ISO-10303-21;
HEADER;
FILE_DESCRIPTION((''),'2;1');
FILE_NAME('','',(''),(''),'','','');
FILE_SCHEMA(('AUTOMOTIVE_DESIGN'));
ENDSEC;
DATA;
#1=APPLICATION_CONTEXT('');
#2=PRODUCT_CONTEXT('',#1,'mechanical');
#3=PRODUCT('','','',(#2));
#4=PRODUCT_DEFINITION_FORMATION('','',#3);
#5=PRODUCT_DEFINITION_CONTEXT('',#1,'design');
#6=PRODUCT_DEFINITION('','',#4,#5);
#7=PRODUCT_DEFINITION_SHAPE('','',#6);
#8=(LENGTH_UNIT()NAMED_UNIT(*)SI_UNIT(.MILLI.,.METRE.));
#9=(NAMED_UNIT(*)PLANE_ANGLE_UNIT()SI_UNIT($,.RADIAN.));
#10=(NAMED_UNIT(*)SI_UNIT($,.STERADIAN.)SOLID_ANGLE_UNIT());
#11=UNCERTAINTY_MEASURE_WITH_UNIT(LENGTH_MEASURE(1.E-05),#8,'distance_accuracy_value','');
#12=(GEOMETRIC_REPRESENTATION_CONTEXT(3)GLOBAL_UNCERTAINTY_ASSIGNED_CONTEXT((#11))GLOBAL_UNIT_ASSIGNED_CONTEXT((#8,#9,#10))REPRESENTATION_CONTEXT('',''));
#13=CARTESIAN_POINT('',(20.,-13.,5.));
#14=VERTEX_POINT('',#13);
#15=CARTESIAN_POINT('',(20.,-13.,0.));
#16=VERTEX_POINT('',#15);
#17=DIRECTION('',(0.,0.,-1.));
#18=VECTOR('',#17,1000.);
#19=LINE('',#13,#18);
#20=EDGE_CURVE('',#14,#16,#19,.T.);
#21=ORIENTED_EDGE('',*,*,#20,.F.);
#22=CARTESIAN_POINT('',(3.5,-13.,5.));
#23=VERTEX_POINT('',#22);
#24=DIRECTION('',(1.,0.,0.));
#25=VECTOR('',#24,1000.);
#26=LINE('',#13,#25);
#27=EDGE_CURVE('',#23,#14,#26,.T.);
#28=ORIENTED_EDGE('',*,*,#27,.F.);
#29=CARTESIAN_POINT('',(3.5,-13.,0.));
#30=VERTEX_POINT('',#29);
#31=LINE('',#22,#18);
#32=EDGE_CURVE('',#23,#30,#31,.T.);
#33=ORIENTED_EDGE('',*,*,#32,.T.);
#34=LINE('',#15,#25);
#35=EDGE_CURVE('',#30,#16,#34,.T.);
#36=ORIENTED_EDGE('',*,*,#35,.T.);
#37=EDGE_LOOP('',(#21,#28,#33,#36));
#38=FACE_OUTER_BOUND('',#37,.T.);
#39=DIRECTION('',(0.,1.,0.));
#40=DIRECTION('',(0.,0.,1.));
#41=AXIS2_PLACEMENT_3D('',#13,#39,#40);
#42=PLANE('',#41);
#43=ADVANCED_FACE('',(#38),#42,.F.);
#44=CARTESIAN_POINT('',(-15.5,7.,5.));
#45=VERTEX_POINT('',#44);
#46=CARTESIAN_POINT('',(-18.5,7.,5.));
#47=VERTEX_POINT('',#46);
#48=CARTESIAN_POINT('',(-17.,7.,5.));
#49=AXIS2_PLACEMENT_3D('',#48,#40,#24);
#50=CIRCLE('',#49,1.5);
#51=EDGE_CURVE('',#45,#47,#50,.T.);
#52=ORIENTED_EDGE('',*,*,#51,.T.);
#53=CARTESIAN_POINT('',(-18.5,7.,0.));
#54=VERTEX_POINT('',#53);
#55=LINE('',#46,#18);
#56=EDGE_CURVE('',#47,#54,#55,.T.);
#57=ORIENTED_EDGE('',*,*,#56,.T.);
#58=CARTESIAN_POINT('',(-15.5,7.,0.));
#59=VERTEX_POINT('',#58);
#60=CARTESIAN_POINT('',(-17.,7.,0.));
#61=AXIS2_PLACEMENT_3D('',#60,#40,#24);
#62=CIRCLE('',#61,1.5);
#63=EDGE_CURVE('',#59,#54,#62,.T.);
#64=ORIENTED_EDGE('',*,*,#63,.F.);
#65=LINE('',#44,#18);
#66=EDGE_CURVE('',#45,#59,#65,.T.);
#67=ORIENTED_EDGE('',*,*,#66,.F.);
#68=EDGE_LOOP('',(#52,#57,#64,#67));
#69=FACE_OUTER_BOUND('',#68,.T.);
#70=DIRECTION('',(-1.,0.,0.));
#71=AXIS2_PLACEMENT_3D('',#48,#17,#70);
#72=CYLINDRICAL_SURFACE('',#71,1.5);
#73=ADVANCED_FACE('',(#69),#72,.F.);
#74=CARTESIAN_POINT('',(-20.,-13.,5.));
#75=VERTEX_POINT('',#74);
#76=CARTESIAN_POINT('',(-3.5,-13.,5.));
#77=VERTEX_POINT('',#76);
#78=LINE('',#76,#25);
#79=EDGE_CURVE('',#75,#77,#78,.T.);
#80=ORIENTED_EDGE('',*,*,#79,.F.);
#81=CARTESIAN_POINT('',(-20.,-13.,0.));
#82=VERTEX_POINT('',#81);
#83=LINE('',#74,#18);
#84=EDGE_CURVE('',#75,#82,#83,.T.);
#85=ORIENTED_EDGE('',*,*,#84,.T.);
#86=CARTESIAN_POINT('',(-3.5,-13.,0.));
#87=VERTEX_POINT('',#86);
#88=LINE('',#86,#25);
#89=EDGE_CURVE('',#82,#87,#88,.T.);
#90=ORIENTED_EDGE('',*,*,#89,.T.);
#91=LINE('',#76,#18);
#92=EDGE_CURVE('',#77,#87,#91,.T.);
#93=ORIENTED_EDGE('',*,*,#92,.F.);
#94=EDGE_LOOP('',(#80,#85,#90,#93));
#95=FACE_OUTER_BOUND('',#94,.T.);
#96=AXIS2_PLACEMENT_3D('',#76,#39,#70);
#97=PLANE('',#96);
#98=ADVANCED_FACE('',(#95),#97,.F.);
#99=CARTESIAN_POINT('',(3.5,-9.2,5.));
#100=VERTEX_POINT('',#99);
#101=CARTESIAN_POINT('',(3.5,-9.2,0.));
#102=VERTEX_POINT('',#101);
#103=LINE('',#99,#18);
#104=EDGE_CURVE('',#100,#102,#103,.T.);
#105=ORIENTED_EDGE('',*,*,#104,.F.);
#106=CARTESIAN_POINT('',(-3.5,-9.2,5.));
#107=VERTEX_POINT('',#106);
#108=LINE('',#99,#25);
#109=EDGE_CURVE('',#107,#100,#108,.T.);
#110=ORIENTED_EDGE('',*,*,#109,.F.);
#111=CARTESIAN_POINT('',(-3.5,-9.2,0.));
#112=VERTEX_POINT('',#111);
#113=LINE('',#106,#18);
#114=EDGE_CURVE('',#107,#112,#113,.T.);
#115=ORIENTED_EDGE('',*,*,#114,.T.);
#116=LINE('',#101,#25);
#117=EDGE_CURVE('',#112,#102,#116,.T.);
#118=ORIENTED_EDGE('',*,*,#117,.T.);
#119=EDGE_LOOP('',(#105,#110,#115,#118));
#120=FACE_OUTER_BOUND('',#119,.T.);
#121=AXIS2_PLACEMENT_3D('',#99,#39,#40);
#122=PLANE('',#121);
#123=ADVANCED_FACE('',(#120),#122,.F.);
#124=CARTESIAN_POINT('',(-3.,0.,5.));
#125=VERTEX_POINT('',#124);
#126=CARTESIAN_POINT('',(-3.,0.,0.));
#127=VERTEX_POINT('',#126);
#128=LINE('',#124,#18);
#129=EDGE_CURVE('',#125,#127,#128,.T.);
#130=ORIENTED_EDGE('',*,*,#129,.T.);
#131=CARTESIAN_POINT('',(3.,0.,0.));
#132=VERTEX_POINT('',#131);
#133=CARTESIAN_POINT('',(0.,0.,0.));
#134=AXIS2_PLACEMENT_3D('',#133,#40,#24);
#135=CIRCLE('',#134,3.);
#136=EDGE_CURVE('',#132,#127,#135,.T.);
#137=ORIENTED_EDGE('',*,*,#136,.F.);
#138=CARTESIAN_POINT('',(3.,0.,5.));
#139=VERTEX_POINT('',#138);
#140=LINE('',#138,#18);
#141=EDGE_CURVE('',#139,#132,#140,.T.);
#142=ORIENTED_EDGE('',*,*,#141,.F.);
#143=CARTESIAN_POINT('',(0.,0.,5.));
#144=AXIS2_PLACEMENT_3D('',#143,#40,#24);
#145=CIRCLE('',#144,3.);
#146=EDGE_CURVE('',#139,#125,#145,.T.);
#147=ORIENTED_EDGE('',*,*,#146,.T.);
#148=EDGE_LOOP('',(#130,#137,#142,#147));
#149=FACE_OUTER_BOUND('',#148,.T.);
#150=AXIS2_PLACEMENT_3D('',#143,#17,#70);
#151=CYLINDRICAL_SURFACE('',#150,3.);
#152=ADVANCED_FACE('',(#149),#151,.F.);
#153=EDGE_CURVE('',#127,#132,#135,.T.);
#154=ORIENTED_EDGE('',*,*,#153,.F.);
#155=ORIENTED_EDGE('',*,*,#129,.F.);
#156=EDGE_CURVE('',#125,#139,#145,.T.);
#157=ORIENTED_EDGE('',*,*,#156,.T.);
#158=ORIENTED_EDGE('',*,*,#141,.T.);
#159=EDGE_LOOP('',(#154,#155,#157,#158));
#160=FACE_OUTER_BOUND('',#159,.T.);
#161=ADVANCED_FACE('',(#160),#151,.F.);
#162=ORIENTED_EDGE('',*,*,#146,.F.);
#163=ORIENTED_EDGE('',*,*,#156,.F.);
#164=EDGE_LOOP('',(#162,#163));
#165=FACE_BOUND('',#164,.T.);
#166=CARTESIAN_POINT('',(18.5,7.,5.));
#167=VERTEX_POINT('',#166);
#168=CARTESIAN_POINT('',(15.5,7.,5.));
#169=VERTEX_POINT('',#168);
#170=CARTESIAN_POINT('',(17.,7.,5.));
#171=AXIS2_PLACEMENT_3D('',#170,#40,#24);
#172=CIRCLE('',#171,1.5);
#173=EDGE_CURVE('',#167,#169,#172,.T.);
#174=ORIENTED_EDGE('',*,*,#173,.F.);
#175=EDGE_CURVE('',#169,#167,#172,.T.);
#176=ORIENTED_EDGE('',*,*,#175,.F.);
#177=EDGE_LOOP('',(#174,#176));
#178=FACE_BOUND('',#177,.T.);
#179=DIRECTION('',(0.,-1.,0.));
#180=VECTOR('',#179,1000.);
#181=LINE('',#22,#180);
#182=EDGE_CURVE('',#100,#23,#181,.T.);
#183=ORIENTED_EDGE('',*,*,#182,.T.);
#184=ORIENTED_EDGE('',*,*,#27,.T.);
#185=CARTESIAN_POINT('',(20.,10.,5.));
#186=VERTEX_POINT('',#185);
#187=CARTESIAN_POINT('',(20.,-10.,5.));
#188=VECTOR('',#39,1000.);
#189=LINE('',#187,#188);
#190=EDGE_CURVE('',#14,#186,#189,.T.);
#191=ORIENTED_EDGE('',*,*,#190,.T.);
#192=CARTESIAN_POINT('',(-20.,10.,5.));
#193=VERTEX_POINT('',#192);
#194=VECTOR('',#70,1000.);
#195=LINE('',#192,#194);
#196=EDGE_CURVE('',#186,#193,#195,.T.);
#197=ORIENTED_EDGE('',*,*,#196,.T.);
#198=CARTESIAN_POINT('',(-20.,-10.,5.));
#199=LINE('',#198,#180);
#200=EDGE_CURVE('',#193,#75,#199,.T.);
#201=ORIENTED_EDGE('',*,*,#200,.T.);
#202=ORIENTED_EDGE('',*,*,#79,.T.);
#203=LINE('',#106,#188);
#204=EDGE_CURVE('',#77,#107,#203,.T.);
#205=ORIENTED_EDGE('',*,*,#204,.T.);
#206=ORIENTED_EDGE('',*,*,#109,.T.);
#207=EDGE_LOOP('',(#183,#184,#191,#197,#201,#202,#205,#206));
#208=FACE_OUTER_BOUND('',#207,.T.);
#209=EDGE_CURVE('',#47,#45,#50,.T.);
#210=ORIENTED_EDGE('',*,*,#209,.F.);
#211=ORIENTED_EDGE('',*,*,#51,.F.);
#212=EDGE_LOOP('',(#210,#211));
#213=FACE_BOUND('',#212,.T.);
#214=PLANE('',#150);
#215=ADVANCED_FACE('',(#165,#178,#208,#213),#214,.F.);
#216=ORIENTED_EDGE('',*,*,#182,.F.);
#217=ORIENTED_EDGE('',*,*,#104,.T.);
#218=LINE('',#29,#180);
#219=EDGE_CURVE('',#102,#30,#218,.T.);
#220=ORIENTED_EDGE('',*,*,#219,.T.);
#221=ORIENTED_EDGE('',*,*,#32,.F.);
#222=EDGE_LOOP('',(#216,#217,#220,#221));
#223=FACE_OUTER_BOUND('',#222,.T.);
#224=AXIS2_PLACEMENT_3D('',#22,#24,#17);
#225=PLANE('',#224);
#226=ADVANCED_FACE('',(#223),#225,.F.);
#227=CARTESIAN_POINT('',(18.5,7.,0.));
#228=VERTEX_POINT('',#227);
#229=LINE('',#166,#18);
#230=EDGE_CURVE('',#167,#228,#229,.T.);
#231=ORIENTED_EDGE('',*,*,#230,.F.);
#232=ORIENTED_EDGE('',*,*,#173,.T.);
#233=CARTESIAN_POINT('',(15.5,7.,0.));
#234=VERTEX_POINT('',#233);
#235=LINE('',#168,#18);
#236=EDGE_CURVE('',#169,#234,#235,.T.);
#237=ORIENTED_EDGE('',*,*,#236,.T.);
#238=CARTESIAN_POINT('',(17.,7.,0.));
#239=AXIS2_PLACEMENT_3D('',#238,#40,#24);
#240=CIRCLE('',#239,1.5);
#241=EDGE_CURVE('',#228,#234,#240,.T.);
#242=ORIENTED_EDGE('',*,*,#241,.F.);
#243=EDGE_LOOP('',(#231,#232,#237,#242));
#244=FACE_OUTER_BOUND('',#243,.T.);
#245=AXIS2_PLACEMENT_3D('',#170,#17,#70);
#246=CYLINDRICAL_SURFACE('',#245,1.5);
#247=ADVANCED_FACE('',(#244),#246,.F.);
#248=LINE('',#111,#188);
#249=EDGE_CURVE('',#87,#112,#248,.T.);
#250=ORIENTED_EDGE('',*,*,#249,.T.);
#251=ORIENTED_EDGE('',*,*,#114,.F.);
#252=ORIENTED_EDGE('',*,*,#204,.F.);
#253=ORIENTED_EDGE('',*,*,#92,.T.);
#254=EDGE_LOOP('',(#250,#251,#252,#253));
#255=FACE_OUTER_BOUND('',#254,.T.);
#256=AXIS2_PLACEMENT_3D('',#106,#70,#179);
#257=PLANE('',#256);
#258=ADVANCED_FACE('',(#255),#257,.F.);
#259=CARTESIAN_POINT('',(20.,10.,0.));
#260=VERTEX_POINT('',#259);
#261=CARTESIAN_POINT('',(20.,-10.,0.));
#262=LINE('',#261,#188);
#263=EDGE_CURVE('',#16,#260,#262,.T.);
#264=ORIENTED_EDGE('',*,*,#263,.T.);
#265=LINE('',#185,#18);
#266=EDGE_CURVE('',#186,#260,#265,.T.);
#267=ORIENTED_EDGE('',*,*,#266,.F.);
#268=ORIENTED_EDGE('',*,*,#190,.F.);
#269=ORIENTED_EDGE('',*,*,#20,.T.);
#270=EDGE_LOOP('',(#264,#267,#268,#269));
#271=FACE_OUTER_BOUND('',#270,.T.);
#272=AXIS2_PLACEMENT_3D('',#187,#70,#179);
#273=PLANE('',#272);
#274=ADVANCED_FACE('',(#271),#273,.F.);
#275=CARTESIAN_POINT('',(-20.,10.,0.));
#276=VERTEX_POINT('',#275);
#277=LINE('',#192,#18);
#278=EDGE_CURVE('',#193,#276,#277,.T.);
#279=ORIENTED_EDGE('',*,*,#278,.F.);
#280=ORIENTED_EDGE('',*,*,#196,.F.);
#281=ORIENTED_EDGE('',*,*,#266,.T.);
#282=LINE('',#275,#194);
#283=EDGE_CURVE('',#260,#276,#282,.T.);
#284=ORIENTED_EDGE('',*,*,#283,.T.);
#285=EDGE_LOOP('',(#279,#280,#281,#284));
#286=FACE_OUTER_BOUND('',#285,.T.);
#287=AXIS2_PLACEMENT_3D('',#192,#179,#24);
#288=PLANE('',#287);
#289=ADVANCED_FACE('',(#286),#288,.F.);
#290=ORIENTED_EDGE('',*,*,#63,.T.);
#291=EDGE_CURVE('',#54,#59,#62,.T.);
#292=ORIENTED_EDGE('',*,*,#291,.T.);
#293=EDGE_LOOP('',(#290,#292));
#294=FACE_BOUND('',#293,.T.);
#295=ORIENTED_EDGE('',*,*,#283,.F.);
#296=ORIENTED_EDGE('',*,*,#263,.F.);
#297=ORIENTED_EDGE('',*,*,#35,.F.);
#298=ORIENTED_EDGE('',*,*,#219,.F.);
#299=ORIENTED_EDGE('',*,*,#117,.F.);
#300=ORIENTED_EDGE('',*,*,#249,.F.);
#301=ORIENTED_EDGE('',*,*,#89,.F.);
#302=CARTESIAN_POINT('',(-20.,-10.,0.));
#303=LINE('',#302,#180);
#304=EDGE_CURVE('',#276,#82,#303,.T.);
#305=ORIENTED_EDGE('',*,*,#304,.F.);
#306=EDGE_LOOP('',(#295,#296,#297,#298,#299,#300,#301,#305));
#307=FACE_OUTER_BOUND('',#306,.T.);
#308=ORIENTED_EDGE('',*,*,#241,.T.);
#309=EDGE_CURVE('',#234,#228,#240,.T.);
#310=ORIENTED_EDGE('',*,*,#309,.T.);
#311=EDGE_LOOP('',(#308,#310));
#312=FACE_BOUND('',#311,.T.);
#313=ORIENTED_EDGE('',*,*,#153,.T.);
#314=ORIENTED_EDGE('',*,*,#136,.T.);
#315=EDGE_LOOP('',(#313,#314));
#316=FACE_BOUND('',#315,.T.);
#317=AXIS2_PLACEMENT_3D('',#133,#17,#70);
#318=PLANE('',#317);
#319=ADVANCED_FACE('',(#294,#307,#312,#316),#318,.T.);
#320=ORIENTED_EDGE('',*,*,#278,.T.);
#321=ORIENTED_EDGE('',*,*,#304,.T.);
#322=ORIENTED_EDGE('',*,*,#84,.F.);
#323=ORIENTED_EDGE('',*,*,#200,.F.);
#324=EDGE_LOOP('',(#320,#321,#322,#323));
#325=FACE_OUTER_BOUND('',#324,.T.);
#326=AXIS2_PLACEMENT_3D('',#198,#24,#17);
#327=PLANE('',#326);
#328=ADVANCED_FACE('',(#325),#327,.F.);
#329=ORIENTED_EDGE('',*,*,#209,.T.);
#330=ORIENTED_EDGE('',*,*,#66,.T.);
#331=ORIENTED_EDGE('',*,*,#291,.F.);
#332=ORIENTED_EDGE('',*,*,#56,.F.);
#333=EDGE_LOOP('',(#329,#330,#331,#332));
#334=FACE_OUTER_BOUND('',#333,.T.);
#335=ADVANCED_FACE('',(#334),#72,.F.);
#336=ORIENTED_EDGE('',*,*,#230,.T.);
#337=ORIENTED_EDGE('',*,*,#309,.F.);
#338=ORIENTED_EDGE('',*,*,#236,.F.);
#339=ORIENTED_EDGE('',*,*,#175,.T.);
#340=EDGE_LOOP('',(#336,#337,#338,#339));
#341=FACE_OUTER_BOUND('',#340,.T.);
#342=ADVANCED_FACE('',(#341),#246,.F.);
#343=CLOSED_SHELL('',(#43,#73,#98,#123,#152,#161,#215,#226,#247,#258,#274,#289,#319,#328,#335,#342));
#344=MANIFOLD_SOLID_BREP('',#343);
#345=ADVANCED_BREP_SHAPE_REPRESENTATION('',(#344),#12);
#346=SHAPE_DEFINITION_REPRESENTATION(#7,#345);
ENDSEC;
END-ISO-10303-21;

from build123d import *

# Parameters (mm, degrees)
SKETCH1_R           = 3
SKETCH1_R_2         = 1.5
BOSS_EXTRUDE1_DEPTH = 5


with BuildPart() as part:
    # Sketch1 → Boss-Extrude1 (new body)
    with BuildSketch(Plane.XY):
        Polygon((-20, -10), (-20, 10), (20, 10), (20, -10), (20, -13), (3.5, -13), (3.5, -9.2), (-3.5, -9.2), (-3.5, -13), (-20, -13), align=None)
        Circle(SKETCH1_R, mode=Mode.SUBTRACT)
        with Locations((-17, 7)):
            Circle(SKETCH1_R_2, mode=Mode.SUBTRACT)
        with Locations((17, 7)):
            Circle(SKETCH1_R_2, mode=Mode.SUBTRACT)
    extrude(amount=BOSS_EXTRUDE1_DEPTH)


solid = part.part
